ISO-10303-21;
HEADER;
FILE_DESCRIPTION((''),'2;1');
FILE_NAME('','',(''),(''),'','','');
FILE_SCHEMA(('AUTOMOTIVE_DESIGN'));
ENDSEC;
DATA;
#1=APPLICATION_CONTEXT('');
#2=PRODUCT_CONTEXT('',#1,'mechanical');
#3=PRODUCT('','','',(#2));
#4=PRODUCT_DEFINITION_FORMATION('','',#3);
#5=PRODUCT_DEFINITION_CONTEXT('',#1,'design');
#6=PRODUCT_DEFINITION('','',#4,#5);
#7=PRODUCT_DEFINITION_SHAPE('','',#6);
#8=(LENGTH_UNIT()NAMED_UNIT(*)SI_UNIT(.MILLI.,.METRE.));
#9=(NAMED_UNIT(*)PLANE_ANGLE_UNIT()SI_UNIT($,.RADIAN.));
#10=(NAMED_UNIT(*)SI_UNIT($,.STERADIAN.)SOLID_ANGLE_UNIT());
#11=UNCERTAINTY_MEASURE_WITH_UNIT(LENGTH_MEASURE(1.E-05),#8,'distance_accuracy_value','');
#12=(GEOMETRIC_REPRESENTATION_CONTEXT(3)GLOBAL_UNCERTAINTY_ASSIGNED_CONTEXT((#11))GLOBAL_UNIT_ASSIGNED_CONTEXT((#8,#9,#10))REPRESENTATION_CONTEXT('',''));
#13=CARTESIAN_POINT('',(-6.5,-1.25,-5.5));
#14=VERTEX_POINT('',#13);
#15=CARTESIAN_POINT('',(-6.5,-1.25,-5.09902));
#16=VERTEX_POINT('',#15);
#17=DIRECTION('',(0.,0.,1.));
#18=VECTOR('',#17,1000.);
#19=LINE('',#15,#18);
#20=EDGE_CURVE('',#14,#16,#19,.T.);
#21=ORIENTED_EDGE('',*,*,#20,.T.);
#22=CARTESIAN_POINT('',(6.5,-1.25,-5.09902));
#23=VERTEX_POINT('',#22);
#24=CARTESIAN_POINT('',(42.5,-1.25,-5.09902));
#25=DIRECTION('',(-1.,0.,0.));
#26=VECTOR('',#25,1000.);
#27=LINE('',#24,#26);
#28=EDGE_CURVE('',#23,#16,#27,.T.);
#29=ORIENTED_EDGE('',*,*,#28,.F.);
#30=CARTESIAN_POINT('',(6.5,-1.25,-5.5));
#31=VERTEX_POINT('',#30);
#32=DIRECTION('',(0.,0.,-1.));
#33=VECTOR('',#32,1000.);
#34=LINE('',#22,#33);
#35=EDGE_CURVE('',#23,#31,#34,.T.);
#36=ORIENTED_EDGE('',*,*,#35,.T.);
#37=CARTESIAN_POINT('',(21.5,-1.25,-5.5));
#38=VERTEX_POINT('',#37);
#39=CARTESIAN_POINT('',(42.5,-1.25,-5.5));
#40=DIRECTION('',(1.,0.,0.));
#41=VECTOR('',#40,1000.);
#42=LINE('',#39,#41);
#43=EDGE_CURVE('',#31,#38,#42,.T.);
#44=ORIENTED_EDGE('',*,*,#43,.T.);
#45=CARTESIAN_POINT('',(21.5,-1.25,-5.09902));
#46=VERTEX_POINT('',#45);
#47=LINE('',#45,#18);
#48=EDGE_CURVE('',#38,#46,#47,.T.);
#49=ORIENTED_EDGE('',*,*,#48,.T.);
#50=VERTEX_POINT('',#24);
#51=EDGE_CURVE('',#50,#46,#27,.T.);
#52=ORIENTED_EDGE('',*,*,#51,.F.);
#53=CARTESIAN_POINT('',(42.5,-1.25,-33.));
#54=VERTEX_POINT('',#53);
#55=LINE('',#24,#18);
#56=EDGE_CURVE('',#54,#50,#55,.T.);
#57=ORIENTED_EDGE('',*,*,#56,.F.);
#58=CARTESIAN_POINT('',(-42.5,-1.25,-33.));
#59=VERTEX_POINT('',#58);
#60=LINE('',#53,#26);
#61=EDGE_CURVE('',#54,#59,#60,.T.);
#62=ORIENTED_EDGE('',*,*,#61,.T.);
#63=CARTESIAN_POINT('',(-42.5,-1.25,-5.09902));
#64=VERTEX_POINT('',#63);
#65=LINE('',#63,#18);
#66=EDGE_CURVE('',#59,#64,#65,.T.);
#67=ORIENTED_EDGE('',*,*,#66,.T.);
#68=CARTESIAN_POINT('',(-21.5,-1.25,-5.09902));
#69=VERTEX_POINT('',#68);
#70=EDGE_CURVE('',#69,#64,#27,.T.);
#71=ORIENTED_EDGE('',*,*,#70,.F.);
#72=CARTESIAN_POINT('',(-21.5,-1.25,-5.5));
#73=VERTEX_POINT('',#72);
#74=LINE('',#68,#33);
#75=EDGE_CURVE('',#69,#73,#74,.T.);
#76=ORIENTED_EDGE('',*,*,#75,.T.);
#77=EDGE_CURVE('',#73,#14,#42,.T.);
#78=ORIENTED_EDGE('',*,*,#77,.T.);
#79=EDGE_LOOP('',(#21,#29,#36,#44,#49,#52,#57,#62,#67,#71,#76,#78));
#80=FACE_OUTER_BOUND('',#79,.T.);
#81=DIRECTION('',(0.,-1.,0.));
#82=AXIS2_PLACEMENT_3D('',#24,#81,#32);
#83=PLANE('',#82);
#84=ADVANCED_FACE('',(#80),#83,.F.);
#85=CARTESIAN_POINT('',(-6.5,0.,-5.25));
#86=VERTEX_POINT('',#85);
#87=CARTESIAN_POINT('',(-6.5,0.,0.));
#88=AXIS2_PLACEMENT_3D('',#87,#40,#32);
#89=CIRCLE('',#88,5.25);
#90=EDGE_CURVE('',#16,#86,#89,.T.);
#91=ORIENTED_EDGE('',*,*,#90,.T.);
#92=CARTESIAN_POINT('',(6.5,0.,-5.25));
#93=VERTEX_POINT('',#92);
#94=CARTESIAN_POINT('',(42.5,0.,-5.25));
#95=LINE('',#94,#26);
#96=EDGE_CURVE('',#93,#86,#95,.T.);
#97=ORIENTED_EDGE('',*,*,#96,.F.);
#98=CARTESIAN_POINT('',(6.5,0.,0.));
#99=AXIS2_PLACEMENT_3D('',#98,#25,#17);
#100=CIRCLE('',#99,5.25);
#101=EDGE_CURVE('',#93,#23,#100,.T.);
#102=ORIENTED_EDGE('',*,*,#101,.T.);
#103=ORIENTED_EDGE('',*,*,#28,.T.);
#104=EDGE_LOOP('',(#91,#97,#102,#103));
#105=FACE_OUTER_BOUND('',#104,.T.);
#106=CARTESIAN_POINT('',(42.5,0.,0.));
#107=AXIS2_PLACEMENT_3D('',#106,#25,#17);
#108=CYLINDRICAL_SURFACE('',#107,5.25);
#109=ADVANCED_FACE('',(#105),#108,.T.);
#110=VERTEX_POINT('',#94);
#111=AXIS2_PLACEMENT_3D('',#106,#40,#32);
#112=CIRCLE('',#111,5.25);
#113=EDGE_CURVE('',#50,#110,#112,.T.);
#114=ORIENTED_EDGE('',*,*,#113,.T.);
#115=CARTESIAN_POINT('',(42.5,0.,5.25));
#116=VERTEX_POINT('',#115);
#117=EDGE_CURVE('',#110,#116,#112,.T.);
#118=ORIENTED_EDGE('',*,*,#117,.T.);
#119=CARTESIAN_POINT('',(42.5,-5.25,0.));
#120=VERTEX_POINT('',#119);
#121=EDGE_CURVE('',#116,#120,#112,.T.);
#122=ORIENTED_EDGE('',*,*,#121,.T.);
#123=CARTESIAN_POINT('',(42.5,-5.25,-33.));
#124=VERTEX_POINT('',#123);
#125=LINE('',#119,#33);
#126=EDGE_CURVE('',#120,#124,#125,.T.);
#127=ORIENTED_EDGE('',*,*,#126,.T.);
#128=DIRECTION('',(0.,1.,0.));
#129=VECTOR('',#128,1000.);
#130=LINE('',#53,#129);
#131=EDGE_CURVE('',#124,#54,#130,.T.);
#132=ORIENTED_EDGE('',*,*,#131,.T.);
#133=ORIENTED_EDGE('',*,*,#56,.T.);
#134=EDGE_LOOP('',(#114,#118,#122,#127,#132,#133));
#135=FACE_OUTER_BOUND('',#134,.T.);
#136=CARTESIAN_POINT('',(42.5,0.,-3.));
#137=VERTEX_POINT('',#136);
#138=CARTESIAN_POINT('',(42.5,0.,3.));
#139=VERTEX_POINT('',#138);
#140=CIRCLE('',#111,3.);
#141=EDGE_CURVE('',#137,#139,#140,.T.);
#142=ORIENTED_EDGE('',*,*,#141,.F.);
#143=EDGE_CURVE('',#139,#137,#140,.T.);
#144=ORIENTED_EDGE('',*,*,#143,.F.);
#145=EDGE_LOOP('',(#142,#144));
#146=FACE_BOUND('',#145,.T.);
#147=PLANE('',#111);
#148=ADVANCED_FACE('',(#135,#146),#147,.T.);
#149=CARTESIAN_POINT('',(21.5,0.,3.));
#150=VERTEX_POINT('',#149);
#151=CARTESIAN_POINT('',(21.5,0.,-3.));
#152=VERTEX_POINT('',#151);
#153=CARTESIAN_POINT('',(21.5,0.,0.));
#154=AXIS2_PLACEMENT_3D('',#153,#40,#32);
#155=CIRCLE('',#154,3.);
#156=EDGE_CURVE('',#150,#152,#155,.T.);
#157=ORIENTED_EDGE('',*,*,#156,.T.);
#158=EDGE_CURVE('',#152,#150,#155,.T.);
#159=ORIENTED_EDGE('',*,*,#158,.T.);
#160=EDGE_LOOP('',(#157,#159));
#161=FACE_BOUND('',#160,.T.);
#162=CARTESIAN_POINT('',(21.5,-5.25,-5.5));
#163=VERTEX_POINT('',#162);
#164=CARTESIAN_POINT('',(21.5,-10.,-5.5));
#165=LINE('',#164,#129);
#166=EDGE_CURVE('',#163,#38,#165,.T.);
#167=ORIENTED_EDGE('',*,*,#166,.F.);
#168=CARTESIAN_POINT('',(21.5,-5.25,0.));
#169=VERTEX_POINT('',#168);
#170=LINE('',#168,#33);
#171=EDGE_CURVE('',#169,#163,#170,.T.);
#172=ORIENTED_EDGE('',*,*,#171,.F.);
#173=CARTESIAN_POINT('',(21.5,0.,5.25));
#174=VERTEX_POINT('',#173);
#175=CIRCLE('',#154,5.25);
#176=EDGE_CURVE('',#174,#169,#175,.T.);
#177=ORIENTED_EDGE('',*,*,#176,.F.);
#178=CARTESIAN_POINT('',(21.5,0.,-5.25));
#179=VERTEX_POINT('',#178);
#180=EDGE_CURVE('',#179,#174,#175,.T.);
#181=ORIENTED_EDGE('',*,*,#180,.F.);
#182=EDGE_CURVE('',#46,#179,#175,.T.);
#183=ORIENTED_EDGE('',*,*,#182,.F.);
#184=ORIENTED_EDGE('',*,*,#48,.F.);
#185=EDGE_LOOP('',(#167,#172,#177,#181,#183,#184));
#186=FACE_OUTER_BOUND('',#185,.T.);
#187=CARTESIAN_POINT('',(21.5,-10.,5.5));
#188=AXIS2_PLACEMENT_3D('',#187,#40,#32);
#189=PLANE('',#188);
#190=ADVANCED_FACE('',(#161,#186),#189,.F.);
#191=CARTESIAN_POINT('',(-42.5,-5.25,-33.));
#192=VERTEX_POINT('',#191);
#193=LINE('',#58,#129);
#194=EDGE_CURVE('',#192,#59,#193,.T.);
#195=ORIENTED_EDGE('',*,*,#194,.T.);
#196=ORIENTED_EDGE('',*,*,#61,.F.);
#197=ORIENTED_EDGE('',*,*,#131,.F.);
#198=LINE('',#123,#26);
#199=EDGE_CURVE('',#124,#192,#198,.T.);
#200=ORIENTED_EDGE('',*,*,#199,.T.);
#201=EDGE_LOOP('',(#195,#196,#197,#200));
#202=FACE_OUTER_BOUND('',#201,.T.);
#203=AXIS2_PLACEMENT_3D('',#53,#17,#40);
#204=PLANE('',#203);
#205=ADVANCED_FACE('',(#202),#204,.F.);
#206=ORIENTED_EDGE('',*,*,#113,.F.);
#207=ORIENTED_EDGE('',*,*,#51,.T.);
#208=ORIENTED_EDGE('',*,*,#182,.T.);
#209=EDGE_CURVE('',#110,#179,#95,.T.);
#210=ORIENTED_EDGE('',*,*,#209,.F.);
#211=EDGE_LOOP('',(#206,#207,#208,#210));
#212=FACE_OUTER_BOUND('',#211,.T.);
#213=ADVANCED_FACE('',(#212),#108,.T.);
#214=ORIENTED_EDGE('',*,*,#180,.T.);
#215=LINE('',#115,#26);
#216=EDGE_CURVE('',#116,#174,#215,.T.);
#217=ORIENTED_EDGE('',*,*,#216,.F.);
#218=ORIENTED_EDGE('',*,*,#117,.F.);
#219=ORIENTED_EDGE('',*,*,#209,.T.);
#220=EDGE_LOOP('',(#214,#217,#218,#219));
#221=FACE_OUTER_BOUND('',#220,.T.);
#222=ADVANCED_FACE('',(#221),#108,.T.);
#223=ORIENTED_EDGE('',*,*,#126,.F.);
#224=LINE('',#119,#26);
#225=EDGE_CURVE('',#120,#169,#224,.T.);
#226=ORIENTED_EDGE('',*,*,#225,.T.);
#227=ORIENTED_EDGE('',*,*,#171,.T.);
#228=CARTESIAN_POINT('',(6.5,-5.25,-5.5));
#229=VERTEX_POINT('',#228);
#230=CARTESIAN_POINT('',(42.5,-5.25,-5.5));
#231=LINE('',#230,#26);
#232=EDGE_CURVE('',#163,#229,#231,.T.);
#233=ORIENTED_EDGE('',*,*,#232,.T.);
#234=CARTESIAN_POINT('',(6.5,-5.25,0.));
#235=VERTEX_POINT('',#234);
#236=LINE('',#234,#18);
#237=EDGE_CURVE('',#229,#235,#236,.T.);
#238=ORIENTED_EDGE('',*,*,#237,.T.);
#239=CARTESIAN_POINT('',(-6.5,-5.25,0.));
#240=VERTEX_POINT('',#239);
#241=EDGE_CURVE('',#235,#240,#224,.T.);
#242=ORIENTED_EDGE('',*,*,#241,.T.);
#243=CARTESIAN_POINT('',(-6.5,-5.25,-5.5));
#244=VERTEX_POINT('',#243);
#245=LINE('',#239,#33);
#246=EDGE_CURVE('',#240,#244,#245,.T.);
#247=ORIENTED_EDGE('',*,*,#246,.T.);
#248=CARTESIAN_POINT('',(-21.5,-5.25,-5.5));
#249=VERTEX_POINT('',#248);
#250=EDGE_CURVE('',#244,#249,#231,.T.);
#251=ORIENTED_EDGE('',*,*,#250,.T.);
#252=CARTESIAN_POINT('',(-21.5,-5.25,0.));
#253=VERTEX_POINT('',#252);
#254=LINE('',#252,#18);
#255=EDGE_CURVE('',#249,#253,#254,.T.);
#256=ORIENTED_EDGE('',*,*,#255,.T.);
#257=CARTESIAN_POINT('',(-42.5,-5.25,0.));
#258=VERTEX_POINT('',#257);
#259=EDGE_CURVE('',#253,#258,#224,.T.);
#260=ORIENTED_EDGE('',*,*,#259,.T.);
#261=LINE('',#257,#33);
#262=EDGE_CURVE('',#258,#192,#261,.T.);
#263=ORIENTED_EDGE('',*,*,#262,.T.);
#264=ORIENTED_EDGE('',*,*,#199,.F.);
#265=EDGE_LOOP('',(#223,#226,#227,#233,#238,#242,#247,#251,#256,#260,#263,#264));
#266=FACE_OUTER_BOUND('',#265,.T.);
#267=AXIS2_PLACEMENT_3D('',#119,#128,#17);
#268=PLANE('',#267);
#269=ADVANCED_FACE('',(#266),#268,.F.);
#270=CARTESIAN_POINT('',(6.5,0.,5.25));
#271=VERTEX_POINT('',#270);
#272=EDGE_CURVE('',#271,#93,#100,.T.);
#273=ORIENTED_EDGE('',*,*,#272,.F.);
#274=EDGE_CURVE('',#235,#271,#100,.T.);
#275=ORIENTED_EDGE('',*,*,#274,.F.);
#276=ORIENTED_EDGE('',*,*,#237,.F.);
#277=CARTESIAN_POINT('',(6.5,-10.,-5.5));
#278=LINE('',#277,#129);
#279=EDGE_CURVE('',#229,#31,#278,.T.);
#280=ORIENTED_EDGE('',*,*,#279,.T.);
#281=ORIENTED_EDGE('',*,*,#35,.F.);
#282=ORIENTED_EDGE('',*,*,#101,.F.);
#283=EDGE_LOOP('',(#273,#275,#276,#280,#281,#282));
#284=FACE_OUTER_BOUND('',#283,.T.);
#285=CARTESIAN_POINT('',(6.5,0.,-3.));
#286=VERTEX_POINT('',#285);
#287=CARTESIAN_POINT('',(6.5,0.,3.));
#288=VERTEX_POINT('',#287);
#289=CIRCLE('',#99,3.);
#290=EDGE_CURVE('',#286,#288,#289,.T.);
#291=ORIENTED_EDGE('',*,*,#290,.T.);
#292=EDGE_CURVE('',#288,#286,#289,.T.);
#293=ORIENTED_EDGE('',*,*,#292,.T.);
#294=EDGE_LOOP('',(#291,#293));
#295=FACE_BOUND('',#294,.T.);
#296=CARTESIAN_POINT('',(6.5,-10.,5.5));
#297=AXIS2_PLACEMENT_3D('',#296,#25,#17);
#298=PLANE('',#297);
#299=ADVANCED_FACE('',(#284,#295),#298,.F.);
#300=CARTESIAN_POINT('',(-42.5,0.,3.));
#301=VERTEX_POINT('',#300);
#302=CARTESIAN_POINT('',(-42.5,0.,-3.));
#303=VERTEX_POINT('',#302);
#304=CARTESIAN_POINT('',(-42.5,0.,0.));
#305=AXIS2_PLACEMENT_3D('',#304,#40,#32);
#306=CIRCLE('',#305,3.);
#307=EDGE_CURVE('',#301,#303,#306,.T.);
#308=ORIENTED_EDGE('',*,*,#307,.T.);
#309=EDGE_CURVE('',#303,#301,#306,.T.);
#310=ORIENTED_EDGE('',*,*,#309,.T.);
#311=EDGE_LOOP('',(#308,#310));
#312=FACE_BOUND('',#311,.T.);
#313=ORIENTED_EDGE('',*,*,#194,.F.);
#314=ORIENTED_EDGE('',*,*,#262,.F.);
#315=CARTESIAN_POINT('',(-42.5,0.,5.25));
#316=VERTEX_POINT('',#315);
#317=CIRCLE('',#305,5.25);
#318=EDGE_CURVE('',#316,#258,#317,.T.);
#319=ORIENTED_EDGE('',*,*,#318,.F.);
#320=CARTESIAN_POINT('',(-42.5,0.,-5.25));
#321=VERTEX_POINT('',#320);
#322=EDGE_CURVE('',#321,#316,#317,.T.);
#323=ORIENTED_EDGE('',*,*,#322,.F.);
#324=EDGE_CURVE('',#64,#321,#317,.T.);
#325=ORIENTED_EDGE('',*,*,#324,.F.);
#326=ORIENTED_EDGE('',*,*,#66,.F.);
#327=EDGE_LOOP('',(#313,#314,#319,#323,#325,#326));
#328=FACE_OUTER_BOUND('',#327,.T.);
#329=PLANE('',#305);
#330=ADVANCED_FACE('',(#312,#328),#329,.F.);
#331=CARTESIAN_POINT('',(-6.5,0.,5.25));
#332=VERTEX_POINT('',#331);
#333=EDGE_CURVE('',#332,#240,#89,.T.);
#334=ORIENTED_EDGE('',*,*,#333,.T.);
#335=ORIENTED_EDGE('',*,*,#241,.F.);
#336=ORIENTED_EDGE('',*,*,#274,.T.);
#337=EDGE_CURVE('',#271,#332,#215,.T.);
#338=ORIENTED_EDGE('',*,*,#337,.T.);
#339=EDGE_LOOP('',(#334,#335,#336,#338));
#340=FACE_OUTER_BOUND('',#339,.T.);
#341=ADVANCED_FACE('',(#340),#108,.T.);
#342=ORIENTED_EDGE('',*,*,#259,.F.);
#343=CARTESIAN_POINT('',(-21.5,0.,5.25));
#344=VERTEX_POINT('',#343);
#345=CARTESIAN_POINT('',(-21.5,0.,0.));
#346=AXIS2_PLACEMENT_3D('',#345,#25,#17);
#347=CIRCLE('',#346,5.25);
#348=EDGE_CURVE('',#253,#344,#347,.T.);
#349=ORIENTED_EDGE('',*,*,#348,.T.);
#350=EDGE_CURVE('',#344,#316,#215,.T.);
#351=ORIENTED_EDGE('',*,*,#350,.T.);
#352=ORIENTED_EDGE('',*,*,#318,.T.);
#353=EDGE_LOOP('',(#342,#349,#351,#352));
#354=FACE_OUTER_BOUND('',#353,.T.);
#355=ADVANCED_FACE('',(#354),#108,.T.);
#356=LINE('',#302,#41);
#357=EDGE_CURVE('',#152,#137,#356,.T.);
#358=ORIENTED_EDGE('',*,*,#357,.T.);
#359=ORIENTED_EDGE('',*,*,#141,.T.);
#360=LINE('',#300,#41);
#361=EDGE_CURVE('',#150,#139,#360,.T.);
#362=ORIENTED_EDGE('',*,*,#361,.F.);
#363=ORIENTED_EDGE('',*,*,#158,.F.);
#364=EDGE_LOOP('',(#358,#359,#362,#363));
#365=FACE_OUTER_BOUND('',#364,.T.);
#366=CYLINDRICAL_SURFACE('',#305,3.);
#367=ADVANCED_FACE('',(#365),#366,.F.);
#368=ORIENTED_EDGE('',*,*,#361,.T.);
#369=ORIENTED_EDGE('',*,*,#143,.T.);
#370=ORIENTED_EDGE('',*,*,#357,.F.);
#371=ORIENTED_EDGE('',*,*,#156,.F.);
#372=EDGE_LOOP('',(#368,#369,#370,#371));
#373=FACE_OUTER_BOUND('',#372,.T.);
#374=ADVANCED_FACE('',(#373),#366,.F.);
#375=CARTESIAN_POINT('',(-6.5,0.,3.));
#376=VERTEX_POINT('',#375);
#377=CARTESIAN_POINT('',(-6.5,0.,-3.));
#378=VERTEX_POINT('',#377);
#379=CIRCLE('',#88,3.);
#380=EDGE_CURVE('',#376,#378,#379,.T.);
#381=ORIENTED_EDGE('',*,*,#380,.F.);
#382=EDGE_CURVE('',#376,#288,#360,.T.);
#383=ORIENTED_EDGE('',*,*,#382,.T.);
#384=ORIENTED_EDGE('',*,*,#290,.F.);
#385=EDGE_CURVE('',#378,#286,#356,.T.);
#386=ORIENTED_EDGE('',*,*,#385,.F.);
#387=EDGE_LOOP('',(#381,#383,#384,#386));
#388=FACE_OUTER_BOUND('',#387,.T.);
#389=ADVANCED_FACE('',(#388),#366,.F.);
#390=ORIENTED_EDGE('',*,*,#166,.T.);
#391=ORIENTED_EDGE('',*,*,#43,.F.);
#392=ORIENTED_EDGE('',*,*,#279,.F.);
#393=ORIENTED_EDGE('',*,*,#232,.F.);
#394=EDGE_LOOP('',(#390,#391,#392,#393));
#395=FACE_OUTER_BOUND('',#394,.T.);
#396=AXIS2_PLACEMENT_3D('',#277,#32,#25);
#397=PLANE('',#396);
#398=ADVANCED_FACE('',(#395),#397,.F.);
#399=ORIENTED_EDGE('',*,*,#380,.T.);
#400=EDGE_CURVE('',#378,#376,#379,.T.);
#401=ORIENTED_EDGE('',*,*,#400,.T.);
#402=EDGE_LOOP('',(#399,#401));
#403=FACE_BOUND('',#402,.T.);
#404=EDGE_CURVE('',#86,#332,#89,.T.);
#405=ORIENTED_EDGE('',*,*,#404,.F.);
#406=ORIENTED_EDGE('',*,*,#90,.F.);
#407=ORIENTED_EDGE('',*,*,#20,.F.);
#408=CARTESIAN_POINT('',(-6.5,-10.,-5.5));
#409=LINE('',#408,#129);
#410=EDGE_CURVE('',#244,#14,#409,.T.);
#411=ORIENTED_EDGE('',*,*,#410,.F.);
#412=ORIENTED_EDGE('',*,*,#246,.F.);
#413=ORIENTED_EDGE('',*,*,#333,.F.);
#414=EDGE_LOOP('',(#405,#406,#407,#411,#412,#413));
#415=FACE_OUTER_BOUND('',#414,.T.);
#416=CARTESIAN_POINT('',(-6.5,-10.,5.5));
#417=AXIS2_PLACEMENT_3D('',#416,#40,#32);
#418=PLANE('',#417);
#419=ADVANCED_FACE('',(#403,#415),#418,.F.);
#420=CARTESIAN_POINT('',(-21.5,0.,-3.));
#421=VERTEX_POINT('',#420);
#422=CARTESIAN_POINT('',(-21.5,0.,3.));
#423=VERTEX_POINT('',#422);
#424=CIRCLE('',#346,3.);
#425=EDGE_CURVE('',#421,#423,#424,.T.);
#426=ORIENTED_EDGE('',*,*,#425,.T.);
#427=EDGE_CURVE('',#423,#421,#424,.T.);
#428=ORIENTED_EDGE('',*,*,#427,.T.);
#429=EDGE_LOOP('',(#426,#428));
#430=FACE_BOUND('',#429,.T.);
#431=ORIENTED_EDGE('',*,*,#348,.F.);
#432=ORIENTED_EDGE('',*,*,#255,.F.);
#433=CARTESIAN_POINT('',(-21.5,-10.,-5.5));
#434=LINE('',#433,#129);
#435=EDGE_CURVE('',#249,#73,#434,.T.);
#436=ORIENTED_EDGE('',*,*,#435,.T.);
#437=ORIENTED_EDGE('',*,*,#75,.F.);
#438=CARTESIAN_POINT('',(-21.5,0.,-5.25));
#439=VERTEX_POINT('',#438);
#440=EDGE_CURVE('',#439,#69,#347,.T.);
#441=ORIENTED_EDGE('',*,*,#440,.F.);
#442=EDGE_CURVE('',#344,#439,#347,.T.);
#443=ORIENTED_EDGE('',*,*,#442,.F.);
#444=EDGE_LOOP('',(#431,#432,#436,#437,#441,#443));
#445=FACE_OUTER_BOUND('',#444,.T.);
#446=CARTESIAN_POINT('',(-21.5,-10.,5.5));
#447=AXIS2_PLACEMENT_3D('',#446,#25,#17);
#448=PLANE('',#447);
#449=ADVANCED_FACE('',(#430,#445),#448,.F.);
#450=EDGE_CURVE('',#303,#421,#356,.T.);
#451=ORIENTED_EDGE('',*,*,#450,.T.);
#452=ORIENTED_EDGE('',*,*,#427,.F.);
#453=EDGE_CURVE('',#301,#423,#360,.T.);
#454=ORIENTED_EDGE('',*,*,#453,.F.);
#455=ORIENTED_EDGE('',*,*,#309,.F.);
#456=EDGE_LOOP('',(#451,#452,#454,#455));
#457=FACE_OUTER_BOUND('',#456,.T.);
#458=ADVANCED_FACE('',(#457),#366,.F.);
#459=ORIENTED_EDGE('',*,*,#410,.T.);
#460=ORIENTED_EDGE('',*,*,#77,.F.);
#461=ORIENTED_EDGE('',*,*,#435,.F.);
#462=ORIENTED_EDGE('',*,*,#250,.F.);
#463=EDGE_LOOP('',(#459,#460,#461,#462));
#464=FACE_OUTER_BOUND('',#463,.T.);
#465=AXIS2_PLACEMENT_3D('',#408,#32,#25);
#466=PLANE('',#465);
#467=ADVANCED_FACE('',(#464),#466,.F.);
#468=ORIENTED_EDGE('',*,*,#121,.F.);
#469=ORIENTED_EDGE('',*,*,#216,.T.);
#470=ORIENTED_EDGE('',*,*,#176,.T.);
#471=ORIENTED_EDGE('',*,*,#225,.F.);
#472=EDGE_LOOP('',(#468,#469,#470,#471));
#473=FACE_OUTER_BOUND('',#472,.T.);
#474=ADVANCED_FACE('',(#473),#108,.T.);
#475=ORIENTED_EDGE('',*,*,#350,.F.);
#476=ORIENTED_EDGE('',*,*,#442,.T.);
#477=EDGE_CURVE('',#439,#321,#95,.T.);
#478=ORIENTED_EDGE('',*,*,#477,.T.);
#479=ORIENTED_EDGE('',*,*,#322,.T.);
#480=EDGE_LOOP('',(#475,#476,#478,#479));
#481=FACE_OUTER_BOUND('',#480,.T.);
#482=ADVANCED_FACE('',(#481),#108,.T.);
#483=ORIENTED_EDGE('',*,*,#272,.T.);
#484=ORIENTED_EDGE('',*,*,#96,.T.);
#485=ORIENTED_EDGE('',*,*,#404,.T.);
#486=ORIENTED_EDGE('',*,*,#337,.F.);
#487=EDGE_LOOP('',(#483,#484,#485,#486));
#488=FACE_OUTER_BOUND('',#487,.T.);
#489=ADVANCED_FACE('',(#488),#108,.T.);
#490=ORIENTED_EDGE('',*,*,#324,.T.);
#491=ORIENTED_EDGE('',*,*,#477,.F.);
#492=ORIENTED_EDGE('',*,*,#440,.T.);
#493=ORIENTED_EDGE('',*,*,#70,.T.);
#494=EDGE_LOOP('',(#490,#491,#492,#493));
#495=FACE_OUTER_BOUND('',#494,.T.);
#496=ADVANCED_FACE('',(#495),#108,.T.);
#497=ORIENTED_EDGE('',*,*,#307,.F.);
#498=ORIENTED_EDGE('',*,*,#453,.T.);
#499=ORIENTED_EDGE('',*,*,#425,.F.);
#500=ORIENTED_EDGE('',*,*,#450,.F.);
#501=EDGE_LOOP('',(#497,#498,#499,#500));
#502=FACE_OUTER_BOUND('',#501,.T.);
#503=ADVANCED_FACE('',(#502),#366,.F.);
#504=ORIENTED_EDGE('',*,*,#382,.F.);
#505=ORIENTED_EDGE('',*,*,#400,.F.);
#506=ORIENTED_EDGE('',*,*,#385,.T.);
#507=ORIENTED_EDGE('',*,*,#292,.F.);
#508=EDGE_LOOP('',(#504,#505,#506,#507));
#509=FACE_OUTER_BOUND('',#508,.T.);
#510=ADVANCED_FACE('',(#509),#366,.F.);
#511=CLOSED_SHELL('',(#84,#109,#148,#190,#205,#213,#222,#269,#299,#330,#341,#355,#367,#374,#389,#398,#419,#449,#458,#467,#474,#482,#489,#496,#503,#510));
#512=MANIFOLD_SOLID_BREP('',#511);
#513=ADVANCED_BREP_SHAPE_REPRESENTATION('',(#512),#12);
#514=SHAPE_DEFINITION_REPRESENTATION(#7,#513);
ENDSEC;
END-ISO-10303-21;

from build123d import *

# Parameters (mm, degrees)
BOSS_EXTRUDE1_DEPTH = 42.5
SKETCH3_W           = 15
SKETCH3_H           = 11
CUT_EXTRUDE2_DEPTH  = 10
SKETCH4_R           = 3
CUT_EXTRUDE3_DEPTH  = 92.332154798


with BuildPart() as part:
    # Sketch1 → Boss-Extrude1 (new, symmetric)
    with BuildSketch(Plane(origin=(0, 0, 0), x_dir=(0, 0, -1), z_dir=(1, 0, 0))):
        with BuildLine():
            Line((5.099019514, -1.25), (33, -1.25))
            Line((33, -1.25), (33, -5.25))
            Line((33, -5.25), (0, -5.25))
            ThreePointArc((0, -5.25), (-3.240370349, 4.13067791), (5.099019514, -1.25))
        make_face()
    extrude(amount=BOSS_EXTRUDE1_DEPTH, both=True)

    # Sketch3 → Cut-Extrude2 (cut, symmetric)
    with BuildSketch(Plane(origin=(0, 0, 0), x_dir=(1, 0, 0), z_dir=(0, 1, 0))):
        with Locations((14, 0)):
            Rectangle(SKETCH3_W, SKETCH3_H)
        with Locations((-14, 0)):
            Rectangle(SKETCH3_W, SKETCH3_H)
    extrude(amount=CUT_EXTRUDE2_DEPTH, both=True, mode=Mode.SUBTRACT)

    # Sketch4 → Cut-Extrude3 (cut, through all)
    with BuildSketch(Plane(origin=(42.5, 0, 0), x_dir=(0, 0, -1), z_dir=(1, 0, 0))):
        Circle(SKETCH4_R)
    extrude(amount=-CUT_EXTRUDE3_DEPTH, mode=Mode.SUBTRACT)


solid = part.part
